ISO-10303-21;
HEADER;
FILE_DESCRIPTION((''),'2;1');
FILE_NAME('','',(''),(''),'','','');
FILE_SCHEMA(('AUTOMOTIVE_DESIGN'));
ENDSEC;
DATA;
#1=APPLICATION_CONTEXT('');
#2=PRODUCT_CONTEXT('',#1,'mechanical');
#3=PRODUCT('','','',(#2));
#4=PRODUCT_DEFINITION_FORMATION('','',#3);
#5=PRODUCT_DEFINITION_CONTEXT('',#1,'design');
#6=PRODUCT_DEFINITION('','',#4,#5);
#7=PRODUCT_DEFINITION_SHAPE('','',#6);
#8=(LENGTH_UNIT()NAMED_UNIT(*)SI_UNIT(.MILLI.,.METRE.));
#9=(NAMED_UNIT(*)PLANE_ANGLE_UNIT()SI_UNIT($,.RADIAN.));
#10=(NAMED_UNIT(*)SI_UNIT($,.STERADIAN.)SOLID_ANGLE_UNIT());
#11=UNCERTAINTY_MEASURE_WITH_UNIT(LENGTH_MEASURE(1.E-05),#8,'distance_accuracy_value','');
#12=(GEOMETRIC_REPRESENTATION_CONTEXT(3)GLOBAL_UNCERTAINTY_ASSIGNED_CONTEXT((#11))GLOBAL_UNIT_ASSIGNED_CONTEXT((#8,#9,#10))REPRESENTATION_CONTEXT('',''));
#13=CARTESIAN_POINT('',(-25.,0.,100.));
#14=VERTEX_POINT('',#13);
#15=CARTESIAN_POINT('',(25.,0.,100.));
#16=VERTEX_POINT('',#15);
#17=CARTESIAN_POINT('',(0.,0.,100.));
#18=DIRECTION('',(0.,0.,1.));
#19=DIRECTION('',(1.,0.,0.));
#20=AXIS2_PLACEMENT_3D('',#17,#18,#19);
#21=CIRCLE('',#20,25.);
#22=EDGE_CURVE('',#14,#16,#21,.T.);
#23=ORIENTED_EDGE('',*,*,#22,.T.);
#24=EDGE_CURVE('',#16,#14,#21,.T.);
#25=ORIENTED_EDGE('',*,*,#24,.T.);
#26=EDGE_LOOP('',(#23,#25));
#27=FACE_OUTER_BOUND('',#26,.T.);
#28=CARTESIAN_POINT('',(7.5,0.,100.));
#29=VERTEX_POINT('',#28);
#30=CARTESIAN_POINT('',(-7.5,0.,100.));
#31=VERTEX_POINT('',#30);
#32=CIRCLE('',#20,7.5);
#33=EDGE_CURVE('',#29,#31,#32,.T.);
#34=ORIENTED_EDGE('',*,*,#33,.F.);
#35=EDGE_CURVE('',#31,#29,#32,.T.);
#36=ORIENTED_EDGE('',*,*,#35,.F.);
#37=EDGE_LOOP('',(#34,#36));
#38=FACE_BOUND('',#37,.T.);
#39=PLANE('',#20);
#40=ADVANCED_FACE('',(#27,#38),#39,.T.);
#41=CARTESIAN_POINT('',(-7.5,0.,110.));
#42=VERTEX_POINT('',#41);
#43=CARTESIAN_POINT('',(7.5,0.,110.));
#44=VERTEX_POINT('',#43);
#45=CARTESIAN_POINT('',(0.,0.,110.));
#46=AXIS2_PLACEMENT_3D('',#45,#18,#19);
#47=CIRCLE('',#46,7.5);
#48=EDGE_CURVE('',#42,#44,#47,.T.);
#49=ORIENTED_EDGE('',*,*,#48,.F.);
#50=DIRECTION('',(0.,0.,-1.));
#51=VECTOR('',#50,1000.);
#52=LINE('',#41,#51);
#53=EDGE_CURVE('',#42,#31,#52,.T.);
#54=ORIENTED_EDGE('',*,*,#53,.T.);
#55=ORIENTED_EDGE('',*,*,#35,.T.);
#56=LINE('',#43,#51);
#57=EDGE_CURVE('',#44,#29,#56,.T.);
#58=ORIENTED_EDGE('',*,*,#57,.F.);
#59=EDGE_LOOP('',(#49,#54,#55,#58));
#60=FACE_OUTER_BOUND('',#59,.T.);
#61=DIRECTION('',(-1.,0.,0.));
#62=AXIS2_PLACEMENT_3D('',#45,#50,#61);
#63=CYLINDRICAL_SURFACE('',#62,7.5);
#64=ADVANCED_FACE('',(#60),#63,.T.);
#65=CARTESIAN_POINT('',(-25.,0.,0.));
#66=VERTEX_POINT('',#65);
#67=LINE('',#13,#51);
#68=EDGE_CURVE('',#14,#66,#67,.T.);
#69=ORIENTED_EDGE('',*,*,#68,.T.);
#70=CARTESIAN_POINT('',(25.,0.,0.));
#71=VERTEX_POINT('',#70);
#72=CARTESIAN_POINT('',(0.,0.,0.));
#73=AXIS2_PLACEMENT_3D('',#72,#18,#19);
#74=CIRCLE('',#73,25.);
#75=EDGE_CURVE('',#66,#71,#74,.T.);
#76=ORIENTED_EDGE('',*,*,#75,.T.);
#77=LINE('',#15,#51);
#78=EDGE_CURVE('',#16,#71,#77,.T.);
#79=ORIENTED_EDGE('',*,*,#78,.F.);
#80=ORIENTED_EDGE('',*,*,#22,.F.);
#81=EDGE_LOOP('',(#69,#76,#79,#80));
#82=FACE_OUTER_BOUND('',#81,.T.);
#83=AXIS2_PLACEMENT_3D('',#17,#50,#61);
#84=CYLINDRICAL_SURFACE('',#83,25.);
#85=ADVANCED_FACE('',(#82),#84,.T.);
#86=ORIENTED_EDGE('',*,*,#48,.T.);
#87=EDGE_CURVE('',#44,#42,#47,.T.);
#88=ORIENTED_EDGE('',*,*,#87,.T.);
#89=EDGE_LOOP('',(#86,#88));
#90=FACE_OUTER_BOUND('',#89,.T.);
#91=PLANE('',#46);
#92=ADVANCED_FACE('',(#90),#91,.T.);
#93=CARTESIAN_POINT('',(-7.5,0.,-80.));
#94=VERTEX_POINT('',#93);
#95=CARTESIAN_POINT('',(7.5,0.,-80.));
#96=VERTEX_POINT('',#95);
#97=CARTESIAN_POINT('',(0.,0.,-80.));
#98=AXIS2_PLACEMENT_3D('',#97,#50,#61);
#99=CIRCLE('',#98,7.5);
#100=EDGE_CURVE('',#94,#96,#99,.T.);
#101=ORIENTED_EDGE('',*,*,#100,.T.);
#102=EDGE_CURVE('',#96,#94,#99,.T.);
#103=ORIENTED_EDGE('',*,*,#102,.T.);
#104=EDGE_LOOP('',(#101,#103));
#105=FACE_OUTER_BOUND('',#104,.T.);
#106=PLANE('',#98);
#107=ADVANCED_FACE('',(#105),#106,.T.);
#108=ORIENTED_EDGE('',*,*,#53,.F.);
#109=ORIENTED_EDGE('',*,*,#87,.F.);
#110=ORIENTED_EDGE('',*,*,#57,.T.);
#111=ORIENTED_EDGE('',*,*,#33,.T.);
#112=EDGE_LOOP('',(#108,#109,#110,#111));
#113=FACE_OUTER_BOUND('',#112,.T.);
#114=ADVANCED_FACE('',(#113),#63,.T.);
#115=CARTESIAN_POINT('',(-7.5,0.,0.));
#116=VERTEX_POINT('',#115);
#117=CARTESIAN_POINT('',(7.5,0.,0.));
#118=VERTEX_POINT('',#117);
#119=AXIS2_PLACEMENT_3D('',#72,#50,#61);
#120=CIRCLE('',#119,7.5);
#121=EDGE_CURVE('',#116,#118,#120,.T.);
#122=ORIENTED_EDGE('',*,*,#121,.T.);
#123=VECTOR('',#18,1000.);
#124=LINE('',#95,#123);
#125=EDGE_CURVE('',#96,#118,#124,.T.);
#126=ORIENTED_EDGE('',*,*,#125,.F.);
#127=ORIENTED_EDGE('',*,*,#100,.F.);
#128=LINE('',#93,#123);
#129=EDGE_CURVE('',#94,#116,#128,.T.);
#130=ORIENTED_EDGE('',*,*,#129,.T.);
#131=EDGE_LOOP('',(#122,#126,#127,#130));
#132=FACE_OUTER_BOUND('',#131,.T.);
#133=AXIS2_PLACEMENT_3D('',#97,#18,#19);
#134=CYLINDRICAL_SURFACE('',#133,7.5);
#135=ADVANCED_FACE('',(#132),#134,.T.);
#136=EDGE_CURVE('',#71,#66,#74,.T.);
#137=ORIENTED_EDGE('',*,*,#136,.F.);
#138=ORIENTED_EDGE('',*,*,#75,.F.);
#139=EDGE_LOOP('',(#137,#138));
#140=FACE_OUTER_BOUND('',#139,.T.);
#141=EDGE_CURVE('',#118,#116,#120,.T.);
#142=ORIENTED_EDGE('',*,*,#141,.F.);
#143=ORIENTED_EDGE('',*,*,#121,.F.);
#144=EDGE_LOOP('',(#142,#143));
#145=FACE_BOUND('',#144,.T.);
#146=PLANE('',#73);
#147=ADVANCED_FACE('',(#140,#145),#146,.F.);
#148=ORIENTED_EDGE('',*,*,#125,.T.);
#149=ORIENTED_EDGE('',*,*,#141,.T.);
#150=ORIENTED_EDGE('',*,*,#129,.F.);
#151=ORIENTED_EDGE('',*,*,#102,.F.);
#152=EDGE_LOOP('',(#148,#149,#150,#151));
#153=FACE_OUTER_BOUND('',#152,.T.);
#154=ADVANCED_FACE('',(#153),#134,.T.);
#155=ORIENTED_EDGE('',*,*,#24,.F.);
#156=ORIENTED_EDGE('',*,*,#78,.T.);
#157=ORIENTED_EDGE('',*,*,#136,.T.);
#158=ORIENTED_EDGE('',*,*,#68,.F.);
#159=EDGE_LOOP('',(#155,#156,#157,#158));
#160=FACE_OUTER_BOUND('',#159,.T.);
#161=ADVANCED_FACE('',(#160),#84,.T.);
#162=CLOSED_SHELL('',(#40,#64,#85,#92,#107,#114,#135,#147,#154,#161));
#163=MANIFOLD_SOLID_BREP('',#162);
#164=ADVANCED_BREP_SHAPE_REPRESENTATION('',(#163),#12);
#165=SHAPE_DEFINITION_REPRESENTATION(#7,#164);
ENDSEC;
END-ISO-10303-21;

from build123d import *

# Parameters (mm, degrees)
SKETCH_1_R      = 25
EXTRUDE_1_DEPTH = 100
SKETCH_2_R      = 7.5
EXTRUDE_2_DEPTH = 10
EXTRUDE_START   = 80
SKETCH_3_R      = 7.5
EXTRUDE_3_DEPTH = 80


with BuildPart() as part:
    # 草图1 → 凸台-拉伸1 (new body)
    with BuildSketch(Plane.XY):
        Circle(SKETCH_1_R)
    extrude(amount=EXTRUDE_1_DEPTH)

    # 草图2 → 凸台-拉伸2 (add)
    with BuildSketch(Plane.XY.offset(100)):
        Circle(SKETCH_2_R)
    extrude(amount=EXTRUDE_2_DEPTH)

    # 草图3 → 凸台-拉伸3 (add)
    with BuildSketch(Plane(origin=(0, 0, 0), x_dir=(-1, 0, 0), z_dir=(0, 0, -1)).offset(EXTRUDE_START)):
        with Locations(Location((0, 0, 0), (0, 0, 180))):
            Circle(SKETCH_3_R)
    extrude(amount=-EXTRUDE_3_DEPTH)


solid = part.part
